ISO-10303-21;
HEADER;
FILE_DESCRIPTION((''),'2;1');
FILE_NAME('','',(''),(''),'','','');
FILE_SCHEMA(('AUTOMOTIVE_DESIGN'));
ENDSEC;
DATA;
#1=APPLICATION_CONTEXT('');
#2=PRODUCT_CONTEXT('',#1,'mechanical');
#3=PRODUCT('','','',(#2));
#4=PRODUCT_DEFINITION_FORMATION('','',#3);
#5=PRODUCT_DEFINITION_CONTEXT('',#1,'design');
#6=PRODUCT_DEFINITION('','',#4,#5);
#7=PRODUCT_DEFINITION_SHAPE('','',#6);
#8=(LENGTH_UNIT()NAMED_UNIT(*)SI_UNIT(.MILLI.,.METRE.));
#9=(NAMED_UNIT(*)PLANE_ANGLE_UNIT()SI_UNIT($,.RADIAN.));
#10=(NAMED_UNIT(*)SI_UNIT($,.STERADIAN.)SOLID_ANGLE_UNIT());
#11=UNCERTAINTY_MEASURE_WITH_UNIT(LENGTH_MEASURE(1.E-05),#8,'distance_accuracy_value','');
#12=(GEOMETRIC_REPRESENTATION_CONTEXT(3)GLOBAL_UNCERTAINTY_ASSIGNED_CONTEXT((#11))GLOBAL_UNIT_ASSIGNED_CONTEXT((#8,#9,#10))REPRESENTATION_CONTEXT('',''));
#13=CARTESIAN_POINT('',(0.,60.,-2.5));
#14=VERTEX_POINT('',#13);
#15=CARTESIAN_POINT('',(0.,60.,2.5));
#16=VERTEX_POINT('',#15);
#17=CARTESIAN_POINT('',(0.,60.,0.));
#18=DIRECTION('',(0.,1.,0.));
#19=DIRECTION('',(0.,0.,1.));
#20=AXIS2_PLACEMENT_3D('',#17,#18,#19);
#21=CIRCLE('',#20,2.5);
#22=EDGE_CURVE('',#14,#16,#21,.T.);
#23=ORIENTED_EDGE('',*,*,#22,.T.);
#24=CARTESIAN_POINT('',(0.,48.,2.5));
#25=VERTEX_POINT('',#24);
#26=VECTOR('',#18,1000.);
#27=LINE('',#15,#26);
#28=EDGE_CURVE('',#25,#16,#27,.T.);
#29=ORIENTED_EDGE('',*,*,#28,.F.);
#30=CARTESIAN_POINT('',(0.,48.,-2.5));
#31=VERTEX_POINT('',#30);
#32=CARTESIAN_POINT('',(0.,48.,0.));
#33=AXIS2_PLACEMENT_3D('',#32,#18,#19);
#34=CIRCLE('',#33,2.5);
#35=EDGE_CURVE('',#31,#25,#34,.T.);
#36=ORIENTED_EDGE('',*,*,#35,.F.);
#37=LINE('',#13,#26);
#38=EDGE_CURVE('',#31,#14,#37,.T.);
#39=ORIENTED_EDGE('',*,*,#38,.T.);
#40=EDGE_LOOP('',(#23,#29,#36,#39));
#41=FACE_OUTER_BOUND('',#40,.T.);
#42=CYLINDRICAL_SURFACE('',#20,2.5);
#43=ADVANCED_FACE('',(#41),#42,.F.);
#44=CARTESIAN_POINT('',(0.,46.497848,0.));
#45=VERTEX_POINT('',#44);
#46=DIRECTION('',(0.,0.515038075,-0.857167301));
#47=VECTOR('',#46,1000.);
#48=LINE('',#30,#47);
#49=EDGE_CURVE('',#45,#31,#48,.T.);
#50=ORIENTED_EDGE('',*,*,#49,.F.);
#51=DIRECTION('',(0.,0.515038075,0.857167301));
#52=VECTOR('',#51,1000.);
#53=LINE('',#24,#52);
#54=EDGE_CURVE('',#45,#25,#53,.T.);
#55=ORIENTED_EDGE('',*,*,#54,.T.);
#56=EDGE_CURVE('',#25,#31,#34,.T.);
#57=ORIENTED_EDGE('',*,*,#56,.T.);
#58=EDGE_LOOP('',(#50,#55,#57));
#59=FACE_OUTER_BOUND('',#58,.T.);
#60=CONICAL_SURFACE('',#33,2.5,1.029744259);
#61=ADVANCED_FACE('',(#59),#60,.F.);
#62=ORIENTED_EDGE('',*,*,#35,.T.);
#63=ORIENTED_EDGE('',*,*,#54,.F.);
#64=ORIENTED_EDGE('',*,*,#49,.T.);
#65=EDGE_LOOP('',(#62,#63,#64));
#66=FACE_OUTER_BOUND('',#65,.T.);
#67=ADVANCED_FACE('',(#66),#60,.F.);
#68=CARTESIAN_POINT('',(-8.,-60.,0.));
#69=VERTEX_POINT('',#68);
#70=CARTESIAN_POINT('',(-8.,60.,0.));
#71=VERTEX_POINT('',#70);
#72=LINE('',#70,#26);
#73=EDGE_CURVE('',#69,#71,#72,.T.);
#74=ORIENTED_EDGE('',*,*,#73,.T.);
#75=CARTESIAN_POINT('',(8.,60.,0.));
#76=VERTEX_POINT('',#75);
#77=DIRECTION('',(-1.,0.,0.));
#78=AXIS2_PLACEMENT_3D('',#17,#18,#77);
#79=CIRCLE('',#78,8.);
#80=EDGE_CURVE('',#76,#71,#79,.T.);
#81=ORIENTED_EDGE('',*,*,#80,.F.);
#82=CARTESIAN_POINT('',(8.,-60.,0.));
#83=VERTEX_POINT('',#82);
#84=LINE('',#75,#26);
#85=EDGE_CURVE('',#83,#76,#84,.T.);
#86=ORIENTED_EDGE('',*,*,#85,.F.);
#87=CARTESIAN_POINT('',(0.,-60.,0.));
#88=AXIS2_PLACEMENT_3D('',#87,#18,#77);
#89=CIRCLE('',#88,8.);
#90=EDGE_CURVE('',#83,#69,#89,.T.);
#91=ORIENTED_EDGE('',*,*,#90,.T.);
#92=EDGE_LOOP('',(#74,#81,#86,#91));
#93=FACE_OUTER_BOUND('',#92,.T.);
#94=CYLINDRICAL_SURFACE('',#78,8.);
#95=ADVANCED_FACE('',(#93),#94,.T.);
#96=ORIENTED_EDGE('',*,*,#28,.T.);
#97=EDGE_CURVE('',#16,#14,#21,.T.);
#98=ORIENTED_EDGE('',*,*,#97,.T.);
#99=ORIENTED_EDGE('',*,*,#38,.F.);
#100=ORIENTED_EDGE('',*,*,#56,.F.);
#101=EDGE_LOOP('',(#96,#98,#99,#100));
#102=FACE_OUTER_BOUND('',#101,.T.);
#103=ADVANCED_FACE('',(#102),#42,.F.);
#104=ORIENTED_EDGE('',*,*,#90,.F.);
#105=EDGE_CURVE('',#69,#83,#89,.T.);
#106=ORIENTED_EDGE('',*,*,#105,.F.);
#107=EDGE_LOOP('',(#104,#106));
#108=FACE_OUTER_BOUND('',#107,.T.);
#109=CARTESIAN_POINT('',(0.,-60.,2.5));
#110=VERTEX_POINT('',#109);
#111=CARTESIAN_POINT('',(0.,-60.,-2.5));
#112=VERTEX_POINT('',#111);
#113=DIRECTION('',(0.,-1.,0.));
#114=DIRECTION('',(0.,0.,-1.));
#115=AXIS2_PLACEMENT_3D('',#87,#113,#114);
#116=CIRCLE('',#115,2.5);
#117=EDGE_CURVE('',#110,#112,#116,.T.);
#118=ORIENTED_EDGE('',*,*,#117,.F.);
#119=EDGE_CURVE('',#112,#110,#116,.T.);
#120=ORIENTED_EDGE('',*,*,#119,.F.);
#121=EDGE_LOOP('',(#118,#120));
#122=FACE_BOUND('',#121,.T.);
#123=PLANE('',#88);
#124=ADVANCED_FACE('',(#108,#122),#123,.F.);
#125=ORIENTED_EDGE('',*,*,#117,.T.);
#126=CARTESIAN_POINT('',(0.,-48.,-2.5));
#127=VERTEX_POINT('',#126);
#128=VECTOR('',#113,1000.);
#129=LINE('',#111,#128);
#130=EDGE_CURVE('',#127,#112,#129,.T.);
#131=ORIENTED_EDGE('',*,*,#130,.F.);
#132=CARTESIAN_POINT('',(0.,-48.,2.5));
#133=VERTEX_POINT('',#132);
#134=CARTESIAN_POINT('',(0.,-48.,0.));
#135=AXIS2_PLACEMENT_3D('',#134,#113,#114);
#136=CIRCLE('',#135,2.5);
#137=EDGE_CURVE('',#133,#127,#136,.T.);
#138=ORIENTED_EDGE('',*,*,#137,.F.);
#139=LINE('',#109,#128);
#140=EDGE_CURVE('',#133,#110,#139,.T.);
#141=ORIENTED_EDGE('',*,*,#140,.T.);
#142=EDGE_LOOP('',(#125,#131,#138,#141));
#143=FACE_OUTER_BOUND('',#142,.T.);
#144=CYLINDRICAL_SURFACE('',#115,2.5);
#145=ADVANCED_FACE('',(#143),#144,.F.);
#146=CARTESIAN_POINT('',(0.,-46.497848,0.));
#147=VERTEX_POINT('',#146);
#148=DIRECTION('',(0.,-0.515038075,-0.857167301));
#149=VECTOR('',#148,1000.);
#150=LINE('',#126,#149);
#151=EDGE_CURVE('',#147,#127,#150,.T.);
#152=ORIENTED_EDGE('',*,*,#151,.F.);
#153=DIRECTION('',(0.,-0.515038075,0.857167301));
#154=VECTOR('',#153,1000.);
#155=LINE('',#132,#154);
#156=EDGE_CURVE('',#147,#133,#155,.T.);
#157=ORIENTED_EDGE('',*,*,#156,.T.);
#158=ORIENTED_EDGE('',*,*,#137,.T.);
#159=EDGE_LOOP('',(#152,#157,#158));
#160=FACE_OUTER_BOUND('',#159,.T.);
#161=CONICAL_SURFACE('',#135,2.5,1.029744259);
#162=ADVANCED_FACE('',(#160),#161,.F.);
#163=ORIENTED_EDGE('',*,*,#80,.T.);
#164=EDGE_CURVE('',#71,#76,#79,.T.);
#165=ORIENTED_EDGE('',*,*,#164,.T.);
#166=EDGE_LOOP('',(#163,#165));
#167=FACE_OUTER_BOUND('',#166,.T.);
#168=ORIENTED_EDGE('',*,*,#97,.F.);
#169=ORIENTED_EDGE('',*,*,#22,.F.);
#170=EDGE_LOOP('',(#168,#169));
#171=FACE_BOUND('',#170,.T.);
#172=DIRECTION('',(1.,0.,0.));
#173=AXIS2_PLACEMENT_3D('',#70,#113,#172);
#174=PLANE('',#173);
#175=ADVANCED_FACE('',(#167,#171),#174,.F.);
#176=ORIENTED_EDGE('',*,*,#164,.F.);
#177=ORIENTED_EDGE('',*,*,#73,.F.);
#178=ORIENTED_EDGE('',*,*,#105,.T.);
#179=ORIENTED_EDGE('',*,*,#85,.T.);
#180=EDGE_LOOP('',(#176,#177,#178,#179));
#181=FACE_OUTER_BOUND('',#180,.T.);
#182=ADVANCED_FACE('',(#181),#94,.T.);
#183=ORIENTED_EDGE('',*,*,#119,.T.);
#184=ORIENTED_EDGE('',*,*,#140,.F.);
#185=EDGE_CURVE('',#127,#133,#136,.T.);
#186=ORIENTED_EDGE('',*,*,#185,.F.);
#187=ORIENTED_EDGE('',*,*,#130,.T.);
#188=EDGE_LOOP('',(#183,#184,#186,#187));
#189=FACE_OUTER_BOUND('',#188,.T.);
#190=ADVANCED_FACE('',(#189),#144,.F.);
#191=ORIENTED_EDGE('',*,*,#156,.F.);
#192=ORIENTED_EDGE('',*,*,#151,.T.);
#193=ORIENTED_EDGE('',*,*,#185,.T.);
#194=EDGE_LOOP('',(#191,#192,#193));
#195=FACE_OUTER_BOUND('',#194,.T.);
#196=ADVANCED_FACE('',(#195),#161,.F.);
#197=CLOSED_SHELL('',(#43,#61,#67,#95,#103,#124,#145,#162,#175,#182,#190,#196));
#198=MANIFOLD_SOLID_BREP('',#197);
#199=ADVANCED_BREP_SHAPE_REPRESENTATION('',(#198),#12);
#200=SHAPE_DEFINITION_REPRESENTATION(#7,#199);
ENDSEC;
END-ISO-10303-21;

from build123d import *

# Parameters (mm, degrees)
SKETCH_1_W             = 8
SKETCH_1_H             = 120
HOLE_WIZARD_M6_1_D     = 5
HOLE_WIZARD_M6_1_DEPTH = 12
HOLE_WIZARD_M6_1_TIP   = 1.502151548
HOLE_WIZARD_M6_2_D     = 5
HOLE_WIZARD_M6_2_DEPTH = 12
HOLE_WIZARD_M6_2_TIP   = 1.502151548


with BuildPart() as part:
    # 草图1 → 旋转-薄壁1 (revolve)
    with BuildSketch(Plane.XY, mode=Mode.PRIVATE) as revolve_1_sk:
        with Locations((4, 0)):
            Rectangle(SKETCH_1_W, SKETCH_1_H)
    revolve(revolve_1_sk.sketch.rotate(Axis((0, 60, 0), (0, -1, 0)), 180), axis=Axis((0, 60, 0), (0, -1, 0)))

    # M6 螺纹孔的螺纹孔钻头1
    with Locations(Plane(origin=(0, 60, 0), x_dir=(1, 0, 0), z_dir=(0, 1, 0))):
        with Locations((0, 0)):
            Hole(HOLE_WIZARD_M6_1_D / 2, depth=HOLE_WIZARD_M6_1_DEPTH)
            with Locations((0, 0, -(HOLE_WIZARD_M6_1_DEPTH + HOLE_WIZARD_M6_1_TIP / 2))):  # 118° drill point
                Cone(0, HOLE_WIZARD_M6_1_D / 2, HOLE_WIZARD_M6_1_TIP, mode=Mode.SUBTRACT)

    # M6 螺纹孔的螺纹孔钻头2
    with Locations(Plane(origin=(0, -60, 0), x_dir=(-1, 0, 0), z_dir=(0, -1, 0))):
        with Locations((0, 0)):
            Hole(HOLE_WIZARD_M6_2_D / 2, depth=HOLE_WIZARD_M6_2_DEPTH)
            with Locations((0, 0, -(HOLE_WIZARD_M6_2_DEPTH + HOLE_WIZARD_M6_2_TIP / 2))):  # 118° drill point
                Cone(0, HOLE_WIZARD_M6_2_D / 2, HOLE_WIZARD_M6_2_TIP, mode=Mode.SUBTRACT)


solid = part.part
